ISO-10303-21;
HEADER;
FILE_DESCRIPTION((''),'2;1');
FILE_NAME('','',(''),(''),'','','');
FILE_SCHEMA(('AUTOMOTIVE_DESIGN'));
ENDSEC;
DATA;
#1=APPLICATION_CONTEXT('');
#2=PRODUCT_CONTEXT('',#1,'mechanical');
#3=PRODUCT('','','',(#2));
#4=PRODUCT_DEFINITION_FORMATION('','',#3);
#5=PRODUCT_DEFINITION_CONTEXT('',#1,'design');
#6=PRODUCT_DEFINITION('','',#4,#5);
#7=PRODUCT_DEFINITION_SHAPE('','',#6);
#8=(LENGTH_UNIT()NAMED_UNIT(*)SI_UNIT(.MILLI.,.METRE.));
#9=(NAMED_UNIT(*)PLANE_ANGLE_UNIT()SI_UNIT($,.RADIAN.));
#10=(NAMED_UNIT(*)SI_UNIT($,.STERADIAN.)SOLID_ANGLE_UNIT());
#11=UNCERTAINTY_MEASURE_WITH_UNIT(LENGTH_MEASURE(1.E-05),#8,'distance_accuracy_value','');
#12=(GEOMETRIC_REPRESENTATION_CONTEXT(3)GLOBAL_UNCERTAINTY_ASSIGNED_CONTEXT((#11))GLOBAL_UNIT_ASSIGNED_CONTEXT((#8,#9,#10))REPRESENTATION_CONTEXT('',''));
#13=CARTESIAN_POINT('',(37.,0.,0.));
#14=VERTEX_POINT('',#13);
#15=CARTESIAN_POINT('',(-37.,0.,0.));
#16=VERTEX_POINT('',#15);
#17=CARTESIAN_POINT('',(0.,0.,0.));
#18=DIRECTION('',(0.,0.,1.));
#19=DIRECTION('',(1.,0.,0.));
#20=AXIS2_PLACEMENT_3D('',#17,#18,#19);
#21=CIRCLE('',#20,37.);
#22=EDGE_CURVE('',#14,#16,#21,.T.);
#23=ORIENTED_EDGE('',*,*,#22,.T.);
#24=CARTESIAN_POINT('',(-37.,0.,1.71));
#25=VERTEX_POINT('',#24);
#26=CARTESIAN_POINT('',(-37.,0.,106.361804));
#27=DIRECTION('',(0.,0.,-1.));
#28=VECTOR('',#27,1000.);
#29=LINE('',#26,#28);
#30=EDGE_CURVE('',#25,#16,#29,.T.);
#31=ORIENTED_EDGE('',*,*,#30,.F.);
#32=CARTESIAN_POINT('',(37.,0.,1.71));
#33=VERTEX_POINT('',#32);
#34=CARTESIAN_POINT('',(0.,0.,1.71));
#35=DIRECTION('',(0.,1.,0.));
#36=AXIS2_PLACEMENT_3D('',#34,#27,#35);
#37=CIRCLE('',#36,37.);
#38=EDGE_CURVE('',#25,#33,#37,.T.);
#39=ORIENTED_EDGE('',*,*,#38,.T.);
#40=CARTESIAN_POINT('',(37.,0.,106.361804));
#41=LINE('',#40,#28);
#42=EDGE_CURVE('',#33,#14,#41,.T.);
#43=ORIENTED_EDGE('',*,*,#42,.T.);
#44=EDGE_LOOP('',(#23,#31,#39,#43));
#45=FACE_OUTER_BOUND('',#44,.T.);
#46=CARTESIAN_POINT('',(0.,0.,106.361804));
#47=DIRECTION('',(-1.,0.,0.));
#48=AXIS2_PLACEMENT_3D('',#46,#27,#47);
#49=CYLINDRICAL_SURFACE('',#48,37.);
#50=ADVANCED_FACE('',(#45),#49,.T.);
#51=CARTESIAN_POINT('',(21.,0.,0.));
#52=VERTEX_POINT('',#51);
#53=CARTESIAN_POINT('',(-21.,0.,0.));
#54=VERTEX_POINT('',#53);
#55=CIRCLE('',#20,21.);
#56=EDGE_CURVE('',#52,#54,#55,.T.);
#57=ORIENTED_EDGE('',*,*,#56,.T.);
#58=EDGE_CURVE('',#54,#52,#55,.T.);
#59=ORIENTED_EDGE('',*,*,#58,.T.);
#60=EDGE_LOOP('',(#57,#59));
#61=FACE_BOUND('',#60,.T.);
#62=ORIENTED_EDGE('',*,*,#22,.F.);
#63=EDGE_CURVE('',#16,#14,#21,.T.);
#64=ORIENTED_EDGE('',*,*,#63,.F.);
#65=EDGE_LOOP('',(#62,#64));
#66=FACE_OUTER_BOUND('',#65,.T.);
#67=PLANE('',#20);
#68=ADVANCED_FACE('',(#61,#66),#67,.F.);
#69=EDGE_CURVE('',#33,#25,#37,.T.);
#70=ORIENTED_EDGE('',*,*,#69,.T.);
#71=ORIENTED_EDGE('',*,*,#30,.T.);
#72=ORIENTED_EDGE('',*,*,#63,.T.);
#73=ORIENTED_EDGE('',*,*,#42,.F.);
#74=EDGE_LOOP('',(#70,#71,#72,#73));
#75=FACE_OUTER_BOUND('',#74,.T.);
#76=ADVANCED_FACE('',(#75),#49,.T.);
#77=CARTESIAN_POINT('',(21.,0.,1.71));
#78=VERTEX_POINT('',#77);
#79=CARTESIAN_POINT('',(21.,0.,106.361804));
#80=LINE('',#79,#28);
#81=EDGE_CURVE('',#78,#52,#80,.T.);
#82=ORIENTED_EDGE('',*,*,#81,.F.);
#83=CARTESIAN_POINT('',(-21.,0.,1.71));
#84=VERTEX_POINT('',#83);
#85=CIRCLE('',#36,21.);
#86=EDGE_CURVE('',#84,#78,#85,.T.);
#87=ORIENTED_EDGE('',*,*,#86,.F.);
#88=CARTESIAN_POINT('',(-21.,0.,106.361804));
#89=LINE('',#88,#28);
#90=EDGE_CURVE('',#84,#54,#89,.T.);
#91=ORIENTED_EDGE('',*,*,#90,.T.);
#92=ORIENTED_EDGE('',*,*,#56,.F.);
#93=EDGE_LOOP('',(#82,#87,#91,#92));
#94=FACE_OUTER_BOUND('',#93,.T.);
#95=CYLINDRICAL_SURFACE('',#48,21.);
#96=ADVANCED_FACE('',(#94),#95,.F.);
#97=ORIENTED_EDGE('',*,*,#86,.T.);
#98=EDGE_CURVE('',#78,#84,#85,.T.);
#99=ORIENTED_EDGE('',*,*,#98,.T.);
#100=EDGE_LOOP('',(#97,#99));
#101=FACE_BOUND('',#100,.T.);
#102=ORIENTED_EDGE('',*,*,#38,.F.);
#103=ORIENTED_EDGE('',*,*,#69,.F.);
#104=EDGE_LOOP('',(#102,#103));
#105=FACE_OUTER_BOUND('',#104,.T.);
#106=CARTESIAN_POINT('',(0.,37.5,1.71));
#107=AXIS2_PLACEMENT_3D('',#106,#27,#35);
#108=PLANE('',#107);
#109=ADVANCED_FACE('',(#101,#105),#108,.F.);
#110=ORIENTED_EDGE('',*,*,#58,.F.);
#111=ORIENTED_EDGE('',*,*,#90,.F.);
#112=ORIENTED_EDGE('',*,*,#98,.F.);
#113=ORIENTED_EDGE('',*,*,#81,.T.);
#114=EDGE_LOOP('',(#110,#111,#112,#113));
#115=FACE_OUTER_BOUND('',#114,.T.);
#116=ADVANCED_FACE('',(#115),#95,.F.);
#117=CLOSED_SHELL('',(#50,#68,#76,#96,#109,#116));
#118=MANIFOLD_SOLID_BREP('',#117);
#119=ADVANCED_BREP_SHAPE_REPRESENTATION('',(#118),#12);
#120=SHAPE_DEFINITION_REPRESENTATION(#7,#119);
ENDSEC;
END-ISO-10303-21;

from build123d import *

# Parameters (mm, degrees)
SKETCH1_R           = 37
SKETCH1_R_2         = 21
BOSS_EXTRUDE1_DEPTH = 1.71


with BuildPart() as part:
    # Sketch1 → Boss-Extrude1 (new body)
    with BuildSketch(Plane.XY):
        with Locations(Location((0, 0, 0), (0, 0, 90))):
            Circle(SKETCH1_R)
        with Locations(Location((0, 0, 0), (0, 0, 90))):
            Circle(SKETCH1_R_2, mode=Mode.SUBTRACT)
    extrude(amount=BOSS_EXTRUDE1_DEPTH)


solid = part.part
